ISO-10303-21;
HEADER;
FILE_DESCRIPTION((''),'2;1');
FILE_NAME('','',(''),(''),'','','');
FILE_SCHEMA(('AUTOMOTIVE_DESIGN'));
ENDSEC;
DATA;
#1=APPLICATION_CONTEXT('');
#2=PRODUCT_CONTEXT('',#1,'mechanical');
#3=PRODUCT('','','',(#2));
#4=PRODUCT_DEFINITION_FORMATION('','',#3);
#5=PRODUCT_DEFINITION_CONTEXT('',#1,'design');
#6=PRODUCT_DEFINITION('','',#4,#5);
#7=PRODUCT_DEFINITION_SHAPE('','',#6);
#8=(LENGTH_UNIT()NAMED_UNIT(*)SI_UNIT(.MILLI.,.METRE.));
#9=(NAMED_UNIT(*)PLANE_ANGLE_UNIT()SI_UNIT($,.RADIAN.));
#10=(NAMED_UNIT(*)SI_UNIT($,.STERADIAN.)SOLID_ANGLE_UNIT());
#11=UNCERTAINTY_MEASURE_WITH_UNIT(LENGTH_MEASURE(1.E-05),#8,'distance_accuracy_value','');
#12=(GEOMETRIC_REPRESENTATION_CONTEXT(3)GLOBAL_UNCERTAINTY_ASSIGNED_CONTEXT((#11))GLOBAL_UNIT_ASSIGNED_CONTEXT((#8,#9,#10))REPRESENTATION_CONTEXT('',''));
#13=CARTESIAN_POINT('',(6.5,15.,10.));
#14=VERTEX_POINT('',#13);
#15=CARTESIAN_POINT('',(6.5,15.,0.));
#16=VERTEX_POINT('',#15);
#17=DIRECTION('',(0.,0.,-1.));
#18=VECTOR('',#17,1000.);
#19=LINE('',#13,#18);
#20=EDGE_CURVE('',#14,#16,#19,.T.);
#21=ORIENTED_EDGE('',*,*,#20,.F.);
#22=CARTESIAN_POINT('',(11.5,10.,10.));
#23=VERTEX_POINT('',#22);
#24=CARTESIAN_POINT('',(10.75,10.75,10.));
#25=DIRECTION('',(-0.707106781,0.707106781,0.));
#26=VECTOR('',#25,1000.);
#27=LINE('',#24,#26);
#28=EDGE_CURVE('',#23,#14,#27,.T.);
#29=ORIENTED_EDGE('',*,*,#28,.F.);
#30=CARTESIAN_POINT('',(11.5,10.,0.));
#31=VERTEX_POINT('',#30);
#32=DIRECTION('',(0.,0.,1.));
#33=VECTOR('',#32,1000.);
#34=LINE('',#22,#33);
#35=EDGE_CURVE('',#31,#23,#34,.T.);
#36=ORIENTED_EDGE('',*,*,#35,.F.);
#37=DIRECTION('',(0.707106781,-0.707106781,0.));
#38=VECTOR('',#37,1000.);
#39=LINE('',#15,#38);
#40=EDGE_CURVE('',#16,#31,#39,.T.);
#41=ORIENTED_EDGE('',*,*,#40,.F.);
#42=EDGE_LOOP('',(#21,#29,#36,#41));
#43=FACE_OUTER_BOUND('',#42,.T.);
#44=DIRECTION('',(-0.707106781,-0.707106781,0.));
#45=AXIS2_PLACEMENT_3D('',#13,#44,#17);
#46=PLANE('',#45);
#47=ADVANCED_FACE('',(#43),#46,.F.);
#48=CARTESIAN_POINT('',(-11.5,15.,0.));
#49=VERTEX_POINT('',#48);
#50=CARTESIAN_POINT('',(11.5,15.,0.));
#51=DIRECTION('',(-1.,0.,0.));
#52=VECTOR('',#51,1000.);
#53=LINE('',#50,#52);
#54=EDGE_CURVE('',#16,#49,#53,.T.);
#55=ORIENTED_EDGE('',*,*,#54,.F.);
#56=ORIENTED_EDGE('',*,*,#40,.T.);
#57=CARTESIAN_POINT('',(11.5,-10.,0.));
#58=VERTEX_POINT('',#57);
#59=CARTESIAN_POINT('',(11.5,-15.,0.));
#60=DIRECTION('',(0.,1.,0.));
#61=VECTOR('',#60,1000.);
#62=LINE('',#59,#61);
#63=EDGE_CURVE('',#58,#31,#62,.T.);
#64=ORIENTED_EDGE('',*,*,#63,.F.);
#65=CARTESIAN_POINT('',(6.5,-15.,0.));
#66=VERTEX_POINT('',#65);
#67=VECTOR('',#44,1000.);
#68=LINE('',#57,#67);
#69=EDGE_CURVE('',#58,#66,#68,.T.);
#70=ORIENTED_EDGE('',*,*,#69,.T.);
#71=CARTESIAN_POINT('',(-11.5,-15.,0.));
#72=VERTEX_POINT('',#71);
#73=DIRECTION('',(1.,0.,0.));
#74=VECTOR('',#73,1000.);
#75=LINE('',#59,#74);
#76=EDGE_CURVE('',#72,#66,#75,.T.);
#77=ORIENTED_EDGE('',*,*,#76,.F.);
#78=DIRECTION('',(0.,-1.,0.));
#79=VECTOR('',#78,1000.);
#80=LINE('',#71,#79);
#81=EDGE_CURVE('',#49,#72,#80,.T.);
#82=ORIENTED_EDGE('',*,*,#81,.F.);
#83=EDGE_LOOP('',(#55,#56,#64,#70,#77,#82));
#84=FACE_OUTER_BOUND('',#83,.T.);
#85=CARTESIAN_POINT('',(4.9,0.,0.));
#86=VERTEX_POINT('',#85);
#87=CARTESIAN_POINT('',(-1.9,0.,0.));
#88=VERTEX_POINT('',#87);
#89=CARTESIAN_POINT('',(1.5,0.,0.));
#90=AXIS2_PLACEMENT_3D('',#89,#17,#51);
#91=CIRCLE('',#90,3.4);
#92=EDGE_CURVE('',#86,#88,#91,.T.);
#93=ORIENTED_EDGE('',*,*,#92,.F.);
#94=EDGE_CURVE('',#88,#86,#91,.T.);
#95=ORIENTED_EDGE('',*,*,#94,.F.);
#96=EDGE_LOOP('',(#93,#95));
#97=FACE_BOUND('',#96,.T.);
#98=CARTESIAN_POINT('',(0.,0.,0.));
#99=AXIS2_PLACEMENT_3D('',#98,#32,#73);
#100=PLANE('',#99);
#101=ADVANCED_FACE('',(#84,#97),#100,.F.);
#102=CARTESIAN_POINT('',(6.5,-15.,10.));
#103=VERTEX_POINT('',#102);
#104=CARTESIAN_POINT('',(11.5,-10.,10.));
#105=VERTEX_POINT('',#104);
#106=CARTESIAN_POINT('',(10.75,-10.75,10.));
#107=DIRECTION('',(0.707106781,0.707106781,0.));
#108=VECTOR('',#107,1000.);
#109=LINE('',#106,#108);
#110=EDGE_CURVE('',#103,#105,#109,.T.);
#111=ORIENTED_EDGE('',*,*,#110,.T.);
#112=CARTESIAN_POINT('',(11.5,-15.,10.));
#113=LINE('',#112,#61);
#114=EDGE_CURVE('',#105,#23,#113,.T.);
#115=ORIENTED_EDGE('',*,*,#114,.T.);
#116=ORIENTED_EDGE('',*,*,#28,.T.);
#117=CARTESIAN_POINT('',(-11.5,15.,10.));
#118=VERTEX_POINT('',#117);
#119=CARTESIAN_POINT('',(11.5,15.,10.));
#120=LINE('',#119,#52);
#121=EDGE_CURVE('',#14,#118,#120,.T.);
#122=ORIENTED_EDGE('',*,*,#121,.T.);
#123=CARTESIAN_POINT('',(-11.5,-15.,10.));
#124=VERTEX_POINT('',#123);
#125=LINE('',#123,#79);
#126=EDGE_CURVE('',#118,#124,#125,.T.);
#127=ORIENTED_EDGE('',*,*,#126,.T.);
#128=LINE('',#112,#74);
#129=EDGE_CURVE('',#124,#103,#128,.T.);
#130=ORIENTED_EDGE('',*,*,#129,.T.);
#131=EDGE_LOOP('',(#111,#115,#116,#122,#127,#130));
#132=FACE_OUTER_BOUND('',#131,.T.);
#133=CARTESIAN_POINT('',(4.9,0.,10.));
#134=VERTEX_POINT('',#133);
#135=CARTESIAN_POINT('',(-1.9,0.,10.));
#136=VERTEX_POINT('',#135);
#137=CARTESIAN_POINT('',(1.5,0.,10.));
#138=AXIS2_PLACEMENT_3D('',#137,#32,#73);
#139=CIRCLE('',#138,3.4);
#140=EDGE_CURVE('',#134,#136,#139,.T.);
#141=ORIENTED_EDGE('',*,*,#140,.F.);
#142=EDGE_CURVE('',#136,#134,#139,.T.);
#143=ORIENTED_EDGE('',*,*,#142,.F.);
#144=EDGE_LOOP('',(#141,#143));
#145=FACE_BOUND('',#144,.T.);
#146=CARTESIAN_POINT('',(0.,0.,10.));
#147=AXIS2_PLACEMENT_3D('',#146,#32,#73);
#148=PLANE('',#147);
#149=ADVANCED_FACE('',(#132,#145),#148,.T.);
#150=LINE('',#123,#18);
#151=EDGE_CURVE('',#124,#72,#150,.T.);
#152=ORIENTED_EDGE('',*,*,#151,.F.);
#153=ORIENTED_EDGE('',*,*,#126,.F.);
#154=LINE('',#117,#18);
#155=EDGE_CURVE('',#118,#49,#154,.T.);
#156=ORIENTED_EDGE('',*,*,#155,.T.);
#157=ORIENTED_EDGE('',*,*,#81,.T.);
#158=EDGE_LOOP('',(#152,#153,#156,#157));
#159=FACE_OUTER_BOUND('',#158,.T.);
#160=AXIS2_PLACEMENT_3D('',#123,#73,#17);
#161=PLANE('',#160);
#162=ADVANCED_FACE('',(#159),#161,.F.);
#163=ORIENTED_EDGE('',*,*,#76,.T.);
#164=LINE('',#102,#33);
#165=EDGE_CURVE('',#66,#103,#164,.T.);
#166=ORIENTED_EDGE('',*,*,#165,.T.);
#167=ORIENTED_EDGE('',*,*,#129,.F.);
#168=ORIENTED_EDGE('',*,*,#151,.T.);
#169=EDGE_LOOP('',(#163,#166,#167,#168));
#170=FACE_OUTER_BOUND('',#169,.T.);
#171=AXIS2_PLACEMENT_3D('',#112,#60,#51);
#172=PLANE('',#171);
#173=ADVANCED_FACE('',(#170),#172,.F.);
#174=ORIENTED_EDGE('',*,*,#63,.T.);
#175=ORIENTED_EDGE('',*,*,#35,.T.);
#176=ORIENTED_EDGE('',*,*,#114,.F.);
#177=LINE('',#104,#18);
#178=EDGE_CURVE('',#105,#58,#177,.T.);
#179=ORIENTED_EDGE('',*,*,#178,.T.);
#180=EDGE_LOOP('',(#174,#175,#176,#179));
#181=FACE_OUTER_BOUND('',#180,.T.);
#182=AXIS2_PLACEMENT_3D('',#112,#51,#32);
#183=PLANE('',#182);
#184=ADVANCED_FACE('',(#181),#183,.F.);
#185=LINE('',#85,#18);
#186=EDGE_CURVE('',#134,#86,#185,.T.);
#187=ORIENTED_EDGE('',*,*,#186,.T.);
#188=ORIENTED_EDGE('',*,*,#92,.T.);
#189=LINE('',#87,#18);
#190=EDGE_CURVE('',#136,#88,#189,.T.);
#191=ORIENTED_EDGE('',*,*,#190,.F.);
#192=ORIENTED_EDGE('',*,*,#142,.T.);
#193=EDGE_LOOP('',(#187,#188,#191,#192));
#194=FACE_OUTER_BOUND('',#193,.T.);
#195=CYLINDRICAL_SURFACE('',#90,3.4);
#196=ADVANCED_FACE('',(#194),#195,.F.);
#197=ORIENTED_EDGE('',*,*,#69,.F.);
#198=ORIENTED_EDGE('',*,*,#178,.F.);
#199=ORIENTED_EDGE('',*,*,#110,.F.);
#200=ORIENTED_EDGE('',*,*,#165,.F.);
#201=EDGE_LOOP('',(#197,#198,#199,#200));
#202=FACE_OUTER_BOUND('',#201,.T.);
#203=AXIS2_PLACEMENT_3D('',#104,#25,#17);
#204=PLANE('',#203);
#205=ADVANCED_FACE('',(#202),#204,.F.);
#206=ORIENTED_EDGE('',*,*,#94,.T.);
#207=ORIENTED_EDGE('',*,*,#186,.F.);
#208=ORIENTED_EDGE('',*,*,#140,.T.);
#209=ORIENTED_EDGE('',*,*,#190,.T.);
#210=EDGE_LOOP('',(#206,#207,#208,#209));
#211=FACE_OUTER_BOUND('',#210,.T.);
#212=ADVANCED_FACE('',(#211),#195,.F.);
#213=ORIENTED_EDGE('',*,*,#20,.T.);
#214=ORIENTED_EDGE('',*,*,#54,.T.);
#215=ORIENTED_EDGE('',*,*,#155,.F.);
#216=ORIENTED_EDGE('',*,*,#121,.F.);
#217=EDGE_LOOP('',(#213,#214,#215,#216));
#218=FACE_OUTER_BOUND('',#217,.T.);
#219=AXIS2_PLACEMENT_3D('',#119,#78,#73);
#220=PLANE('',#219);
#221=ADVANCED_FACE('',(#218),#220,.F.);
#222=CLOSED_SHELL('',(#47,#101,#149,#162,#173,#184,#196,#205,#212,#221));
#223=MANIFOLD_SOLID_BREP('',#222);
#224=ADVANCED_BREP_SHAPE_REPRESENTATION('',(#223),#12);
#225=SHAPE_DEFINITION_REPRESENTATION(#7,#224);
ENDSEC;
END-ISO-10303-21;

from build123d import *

# Parameters (mm, degrees)
SKETCH_1_W         = 23
SKETCH_1_H         = 30
EXTRUDE_1_DEPTH    = 10
CHAMFER_1_SIZE     = 5
HOLE_WIZARD_M8_1_D = 6.8


with BuildPart() as part:
    # 草图1 → 凸台-拉伸1 (new body)
    with BuildSketch(Plane.XY):
        Rectangle(SKETCH_1_W, SKETCH_1_H)
    extrude(amount=EXTRUDE_1_DEPTH)

    # 倒角1
    chamfer_1_edges = [part.edges().sort_by_distance(p)[0] for p in [
        (11.5, 15, 5),
        (11.5, -15, 5),
    ]]
    chamfer(chamfer_1_edges, length=CHAMFER_1_SIZE)

    # M8 螺纹孔1 (through all)
    with Locations(Plane(origin=(0, 0, 0), x_dir=(-1, 0, 0), z_dir=(0, 0, -1))):
        with Locations((-1.5, 0)):
            Hole(HOLE_WIZARD_M8_1_D / 2)


solid = part.part
